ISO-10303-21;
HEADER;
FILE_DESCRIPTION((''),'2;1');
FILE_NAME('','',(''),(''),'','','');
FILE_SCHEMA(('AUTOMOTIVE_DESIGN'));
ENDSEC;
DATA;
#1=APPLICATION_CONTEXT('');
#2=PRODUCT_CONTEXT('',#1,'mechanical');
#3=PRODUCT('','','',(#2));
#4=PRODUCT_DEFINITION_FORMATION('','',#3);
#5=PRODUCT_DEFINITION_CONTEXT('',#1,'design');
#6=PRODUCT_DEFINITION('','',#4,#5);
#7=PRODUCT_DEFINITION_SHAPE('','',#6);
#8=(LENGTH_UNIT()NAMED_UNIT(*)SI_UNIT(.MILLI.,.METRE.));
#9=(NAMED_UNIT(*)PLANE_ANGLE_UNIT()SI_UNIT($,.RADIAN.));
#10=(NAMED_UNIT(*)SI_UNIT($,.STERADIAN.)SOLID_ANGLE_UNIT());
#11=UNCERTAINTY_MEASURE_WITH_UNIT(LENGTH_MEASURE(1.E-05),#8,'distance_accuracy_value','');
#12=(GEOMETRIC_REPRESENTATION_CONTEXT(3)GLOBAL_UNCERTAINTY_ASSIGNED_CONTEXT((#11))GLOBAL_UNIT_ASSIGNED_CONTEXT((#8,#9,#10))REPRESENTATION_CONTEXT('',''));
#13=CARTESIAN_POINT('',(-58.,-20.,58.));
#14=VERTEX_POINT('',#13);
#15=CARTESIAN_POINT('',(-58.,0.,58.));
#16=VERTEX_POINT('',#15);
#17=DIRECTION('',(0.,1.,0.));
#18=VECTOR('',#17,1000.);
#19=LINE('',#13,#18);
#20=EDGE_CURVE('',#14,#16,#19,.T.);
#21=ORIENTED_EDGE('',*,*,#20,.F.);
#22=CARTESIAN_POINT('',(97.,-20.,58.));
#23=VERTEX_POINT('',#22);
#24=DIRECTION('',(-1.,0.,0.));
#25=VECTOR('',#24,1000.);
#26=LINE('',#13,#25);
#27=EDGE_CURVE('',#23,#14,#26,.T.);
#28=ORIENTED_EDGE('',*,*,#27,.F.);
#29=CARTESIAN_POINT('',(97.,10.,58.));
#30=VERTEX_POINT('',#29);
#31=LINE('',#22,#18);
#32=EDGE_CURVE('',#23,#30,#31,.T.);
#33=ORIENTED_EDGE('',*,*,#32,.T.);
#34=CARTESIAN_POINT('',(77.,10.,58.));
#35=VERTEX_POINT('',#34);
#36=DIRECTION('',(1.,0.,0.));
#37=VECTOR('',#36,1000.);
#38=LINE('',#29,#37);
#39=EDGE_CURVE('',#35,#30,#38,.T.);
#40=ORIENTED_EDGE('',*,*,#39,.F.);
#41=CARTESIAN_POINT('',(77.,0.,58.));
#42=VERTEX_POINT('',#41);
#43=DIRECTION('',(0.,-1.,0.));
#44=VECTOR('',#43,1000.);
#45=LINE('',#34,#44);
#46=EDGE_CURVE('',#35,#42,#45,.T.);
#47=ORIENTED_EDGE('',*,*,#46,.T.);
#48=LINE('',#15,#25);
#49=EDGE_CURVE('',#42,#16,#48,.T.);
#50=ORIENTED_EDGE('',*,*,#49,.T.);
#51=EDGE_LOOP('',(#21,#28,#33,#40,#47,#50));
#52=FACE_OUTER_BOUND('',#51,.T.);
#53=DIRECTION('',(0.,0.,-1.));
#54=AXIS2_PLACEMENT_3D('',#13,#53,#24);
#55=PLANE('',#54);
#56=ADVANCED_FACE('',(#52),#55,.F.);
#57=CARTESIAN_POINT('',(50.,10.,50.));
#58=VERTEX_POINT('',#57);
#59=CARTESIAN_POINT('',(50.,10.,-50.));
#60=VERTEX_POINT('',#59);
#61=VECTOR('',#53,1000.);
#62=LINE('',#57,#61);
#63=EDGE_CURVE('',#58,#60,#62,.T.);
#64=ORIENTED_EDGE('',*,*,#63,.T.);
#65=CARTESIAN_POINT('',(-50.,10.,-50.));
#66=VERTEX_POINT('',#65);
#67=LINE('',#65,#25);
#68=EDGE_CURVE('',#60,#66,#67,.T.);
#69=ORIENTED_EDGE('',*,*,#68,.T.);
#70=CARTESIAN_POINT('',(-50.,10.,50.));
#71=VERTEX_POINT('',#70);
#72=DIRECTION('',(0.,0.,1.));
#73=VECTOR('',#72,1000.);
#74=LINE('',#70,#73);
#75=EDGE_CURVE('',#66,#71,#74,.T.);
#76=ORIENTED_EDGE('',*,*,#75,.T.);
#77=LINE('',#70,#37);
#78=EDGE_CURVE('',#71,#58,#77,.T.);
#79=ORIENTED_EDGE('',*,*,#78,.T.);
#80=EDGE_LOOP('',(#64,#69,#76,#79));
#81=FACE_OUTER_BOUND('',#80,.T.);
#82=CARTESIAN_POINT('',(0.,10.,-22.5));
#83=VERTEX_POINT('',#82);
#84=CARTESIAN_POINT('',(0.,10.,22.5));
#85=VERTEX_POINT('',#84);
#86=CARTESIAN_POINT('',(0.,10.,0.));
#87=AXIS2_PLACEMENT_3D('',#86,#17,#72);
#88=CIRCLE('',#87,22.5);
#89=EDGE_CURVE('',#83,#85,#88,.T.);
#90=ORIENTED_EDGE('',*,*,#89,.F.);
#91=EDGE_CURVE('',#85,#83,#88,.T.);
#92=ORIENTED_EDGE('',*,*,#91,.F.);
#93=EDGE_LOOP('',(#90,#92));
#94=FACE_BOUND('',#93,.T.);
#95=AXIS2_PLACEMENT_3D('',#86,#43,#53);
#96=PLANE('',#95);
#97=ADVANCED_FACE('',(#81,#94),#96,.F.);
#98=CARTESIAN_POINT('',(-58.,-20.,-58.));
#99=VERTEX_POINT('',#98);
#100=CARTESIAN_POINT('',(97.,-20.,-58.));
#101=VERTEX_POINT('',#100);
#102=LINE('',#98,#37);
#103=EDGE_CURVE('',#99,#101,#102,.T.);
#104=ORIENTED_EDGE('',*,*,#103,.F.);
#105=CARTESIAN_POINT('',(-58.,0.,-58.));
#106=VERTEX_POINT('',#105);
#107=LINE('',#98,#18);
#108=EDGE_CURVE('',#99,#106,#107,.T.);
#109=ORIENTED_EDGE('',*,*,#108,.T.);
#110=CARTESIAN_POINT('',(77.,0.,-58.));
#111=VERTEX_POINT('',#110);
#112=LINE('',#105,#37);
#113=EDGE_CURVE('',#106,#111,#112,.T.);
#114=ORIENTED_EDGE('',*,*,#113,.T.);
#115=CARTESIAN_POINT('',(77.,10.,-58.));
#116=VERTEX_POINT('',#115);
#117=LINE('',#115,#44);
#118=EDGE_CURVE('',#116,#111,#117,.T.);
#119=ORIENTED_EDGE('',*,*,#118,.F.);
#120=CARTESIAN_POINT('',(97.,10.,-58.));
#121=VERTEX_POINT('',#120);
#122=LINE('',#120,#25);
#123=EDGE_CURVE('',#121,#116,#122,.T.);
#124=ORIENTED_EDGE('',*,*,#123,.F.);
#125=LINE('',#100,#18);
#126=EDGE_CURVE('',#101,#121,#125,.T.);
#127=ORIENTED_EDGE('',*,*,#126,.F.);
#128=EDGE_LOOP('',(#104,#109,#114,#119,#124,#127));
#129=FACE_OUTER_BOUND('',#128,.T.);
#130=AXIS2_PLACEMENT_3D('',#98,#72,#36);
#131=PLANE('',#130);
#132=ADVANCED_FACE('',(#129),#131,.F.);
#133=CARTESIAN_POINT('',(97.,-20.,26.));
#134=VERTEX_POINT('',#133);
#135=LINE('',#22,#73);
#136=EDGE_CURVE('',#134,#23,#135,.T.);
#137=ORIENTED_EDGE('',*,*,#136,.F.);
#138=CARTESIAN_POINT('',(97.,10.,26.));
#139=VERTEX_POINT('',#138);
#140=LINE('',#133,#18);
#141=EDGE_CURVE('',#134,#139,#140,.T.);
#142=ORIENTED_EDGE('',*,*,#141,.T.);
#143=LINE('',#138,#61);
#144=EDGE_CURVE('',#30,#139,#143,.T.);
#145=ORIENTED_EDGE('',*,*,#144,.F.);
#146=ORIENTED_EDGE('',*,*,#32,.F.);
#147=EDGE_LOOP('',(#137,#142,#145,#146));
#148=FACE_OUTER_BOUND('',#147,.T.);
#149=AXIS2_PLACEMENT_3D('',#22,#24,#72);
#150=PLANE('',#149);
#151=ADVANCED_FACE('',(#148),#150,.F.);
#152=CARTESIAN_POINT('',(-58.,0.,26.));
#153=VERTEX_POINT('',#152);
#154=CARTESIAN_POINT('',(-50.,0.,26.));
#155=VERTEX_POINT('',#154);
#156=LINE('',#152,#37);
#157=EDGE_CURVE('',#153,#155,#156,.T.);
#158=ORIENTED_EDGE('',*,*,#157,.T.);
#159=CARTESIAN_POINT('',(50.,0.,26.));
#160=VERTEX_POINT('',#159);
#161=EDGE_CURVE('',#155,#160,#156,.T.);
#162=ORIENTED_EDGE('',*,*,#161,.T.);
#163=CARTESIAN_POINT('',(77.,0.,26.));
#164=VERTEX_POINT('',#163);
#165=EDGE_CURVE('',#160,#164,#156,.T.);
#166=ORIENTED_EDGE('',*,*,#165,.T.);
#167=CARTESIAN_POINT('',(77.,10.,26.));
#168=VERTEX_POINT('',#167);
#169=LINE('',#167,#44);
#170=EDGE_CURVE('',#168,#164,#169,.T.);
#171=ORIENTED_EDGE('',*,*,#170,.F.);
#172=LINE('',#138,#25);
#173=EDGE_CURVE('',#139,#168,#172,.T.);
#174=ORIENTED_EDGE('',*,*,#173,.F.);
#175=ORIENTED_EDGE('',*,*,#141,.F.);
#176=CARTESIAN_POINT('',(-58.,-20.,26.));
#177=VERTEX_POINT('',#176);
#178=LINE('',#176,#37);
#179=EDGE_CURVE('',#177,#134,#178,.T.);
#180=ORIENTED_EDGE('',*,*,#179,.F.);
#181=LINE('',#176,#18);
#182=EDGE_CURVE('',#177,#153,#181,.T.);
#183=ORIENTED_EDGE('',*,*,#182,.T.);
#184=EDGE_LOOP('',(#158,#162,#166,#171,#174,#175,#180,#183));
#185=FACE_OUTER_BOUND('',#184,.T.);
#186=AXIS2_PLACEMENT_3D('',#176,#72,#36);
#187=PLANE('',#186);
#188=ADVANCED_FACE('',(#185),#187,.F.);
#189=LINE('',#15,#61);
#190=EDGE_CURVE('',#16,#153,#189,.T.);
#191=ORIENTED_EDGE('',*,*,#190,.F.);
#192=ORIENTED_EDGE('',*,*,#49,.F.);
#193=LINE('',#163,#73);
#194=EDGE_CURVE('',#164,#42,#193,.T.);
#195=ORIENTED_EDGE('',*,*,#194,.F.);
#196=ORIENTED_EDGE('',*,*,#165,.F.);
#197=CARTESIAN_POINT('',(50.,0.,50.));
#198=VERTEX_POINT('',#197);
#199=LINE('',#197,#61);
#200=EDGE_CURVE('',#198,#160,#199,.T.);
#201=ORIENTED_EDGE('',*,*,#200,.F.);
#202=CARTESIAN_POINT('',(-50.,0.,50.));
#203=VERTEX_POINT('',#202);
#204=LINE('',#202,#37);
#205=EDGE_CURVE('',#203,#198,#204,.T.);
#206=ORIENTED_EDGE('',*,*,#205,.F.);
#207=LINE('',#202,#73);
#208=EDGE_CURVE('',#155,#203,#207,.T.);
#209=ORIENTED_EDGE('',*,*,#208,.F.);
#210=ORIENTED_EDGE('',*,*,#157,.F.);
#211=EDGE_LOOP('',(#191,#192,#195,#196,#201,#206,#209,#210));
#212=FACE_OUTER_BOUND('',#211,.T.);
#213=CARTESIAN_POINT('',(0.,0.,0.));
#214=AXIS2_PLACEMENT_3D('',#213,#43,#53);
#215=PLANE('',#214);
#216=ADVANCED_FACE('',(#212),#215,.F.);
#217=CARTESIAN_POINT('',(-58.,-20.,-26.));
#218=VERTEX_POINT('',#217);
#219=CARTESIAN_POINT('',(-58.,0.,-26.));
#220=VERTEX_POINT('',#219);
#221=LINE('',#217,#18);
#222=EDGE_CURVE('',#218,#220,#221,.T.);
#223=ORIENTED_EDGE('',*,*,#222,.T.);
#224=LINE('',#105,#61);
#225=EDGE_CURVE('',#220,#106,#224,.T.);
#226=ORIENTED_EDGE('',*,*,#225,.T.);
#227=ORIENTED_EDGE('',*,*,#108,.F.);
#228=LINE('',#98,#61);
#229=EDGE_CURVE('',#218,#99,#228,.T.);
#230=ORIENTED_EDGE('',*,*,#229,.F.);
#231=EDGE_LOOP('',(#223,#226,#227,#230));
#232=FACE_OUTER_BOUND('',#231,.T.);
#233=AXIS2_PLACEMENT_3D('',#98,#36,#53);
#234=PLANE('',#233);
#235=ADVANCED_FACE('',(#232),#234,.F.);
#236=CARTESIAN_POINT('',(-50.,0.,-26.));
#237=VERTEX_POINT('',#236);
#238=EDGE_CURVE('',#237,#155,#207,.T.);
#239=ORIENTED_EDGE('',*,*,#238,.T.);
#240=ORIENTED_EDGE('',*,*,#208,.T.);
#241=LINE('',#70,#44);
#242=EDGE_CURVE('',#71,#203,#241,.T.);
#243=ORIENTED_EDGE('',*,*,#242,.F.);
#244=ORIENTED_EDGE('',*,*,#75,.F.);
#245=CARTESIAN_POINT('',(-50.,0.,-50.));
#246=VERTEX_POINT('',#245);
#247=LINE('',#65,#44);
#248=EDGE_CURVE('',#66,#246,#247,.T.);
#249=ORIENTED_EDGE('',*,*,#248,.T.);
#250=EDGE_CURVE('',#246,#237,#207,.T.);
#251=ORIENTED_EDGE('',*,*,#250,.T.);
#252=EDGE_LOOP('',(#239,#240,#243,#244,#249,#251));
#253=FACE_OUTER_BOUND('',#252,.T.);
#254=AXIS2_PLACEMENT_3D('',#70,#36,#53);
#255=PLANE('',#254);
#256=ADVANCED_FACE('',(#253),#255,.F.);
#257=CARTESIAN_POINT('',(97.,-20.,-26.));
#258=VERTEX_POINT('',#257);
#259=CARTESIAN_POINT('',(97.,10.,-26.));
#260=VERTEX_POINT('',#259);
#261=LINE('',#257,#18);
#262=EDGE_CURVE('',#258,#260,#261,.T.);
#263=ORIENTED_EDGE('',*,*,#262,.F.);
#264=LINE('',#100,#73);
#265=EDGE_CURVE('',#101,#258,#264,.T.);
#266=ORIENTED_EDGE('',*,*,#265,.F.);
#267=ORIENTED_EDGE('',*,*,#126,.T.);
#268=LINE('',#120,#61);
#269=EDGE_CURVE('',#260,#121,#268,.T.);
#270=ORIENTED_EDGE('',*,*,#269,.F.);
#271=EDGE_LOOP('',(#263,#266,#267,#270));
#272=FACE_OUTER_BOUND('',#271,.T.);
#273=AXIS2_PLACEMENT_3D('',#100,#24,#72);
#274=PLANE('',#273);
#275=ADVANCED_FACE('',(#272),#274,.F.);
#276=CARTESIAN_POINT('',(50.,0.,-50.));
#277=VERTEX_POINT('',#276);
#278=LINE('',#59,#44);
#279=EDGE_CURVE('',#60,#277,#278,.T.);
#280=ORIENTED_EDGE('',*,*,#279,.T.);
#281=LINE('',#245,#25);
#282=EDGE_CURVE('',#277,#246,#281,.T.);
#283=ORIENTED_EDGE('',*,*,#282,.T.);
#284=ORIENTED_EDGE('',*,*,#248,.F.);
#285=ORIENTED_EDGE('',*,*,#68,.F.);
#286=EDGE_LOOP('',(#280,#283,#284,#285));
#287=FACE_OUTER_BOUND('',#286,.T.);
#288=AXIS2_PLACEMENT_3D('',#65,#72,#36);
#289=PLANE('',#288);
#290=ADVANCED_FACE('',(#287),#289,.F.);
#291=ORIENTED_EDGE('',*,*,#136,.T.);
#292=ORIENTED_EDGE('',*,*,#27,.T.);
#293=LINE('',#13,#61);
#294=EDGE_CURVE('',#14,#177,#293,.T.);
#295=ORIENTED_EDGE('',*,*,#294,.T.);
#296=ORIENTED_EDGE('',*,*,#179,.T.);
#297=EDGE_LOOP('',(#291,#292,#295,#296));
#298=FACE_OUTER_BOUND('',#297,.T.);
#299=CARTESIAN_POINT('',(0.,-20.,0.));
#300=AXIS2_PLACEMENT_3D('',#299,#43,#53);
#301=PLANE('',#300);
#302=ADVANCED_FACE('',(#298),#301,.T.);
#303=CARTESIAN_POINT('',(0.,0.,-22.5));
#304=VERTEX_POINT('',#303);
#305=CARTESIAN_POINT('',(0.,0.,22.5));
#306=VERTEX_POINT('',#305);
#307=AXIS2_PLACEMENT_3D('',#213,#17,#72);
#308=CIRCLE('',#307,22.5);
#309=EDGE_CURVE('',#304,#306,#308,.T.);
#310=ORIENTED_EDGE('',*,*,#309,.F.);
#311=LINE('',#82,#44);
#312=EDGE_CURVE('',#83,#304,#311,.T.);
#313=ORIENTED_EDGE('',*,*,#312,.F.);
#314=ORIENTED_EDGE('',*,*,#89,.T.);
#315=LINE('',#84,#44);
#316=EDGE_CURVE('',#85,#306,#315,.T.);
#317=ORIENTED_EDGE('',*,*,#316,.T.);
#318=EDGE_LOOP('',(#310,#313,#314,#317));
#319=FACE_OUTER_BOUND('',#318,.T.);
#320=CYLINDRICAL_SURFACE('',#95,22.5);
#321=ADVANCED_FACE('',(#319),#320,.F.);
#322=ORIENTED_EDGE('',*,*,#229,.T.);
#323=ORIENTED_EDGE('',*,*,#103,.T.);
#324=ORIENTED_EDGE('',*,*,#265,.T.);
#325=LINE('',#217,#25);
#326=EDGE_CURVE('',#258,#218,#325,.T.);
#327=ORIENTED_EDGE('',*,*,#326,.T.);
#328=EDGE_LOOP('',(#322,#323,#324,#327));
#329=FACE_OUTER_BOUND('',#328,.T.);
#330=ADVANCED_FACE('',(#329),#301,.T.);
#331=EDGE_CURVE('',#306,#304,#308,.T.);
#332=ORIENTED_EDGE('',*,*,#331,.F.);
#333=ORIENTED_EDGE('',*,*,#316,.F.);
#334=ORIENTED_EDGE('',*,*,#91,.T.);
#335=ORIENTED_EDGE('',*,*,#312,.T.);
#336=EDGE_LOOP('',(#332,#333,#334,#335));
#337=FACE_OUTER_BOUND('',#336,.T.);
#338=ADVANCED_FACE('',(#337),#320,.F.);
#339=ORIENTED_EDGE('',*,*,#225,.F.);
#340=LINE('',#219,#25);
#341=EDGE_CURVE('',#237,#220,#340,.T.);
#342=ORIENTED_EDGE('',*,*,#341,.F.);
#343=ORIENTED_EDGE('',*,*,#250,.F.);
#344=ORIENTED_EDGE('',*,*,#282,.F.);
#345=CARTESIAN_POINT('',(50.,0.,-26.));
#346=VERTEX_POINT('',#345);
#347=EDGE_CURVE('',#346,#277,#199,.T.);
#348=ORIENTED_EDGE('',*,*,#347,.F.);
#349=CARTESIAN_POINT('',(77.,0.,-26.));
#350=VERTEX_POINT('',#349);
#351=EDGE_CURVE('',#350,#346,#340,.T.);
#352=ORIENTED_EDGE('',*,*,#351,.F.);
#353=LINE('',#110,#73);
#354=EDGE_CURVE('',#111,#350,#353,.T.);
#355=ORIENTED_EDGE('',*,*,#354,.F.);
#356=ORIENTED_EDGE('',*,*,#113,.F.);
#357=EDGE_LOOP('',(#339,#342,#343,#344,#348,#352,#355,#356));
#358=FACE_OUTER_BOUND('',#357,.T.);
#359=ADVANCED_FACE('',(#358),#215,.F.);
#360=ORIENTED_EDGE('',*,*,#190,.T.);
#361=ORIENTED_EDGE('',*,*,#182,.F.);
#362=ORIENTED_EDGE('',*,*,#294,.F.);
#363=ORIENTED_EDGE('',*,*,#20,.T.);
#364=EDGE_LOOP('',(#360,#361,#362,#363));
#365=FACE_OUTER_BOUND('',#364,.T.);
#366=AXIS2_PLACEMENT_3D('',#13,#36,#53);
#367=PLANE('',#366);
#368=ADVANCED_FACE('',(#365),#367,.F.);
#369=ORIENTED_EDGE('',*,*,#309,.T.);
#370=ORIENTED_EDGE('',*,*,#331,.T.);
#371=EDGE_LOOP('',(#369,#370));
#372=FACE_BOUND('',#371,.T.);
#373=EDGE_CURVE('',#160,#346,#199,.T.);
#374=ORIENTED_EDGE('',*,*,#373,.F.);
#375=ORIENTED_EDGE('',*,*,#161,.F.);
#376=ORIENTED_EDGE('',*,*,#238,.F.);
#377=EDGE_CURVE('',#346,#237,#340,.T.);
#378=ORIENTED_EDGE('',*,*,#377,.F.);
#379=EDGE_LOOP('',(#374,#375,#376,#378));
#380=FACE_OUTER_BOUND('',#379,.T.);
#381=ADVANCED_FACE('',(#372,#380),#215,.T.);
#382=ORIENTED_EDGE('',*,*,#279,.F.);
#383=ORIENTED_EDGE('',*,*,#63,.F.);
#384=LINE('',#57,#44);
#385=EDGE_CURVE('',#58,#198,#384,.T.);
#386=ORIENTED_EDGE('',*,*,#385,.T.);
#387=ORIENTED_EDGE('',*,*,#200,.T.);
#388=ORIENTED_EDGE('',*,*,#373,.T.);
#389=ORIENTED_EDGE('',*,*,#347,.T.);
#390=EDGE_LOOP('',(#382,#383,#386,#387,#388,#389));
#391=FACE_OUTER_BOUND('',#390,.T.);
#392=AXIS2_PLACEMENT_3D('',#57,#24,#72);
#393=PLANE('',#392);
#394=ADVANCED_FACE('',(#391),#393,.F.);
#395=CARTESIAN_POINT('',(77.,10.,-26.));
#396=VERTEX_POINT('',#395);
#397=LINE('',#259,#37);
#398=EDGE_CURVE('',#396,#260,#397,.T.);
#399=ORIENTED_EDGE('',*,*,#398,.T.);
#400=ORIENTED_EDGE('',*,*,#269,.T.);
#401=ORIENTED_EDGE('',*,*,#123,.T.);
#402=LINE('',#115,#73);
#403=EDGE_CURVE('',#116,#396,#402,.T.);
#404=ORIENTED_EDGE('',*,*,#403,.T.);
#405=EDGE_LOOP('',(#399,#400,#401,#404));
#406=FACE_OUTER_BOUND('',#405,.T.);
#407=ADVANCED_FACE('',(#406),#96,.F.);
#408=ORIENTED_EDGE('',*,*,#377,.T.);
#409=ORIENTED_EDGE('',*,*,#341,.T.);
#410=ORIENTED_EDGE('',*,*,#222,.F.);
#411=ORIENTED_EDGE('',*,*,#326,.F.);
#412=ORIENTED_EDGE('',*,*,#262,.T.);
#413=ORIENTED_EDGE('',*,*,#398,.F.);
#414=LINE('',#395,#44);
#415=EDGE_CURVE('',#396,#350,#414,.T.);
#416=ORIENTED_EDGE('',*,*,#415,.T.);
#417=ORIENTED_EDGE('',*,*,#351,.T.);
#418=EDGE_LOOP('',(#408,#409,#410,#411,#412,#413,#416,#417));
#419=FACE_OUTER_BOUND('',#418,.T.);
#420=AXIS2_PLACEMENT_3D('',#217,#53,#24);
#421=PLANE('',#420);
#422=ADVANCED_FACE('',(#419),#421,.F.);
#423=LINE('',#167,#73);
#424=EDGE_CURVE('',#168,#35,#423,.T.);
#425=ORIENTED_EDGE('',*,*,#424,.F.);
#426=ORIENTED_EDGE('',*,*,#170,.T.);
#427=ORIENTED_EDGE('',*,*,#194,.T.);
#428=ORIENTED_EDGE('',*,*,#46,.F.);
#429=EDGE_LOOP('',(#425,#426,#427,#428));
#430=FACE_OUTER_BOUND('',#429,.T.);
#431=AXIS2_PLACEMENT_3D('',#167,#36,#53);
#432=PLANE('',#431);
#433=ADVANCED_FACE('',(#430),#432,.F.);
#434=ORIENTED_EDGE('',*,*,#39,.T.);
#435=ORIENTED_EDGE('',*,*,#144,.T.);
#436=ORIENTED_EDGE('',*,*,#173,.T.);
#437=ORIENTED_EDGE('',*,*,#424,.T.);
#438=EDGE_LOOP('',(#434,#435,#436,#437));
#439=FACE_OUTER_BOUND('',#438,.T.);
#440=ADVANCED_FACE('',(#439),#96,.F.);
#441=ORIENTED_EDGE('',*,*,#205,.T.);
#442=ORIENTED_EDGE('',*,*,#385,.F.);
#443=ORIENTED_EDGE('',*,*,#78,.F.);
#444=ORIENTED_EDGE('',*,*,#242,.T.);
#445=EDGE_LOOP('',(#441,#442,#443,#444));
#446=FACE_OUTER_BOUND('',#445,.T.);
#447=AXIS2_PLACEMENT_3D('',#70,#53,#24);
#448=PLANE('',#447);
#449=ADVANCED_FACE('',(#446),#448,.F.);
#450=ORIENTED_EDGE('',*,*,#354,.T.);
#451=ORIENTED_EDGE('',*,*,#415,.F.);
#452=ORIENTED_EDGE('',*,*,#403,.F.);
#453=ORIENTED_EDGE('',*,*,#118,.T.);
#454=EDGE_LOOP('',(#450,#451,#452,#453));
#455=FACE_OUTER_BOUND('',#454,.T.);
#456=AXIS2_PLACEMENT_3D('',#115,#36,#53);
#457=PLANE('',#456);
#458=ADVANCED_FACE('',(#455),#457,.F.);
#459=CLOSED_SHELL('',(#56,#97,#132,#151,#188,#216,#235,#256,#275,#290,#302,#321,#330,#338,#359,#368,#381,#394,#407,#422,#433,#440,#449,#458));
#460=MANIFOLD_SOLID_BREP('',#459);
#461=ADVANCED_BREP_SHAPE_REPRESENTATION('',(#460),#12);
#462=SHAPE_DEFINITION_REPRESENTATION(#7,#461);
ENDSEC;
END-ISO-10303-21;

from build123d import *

# Parameters (mm, degrees)
BASE_PLATE_SKETCH_W              = 100
BASE_PLATE_SKETCH_H              = 100
BASE_PLATE_SKETCH_R              = 22.5
BASE_PLATE_100X100_BORE_45_DEPTH = 10
SIDE_RAILS_SKETCH_W              = 155
SIDE_RAILS_SKETCH_H              = 32
SIDE_RAILS_DEPTH                 = 20
END_BLOCKS_SKETCH_W              = 20
END_BLOCKS_SKETCH_H              = 32
END_BLOCKS_20X20_DEPTH           = 10


with BuildPart() as part:
    # Base Plate Sketch → Base Plate 100x100 Bore Ø45 (new body)
    with BuildSketch(Plane(origin=(0, 0, 0), x_dir=(1, 0, 0), z_dir=(0, 1, 0))):
        Rectangle(BASE_PLATE_SKETCH_W, BASE_PLATE_SKETCH_H)
        with Locations(Location((0, 0, 0), (0, 0, 270))):
            Circle(BASE_PLATE_SKETCH_R, mode=Mode.SUBTRACT)
    extrude(amount=BASE_PLATE_100X100_BORE_45_DEPTH)

    # Side Rails Sketch → Side Rails (add)
    with BuildSketch(Plane.XZ):
        with Locations((19.5, 42)):
            Rectangle(SIDE_RAILS_SKETCH_W, SIDE_RAILS_SKETCH_H)
        with Locations((19.5, -42)):
            Rectangle(SIDE_RAILS_SKETCH_W, SIDE_RAILS_SKETCH_H)
    extrude(amount=SIDE_RAILS_DEPTH)

    # End Blocks Sketch → End Blocks 20x20 (add)
    with BuildSketch(Plane(origin=(0, 0, 0), x_dir=(1, 0, 0), z_dir=(0, 1, 0))):
        with Locations((87, 42)):
            Rectangle(END_BLOCKS_SKETCH_W, END_BLOCKS_SKETCH_H)
        with Locations((87, -42)):
            Rectangle(END_BLOCKS_SKETCH_W, END_BLOCKS_SKETCH_H)
    extrude(amount=END_BLOCKS_20X20_DEPTH)


solid = part.part
